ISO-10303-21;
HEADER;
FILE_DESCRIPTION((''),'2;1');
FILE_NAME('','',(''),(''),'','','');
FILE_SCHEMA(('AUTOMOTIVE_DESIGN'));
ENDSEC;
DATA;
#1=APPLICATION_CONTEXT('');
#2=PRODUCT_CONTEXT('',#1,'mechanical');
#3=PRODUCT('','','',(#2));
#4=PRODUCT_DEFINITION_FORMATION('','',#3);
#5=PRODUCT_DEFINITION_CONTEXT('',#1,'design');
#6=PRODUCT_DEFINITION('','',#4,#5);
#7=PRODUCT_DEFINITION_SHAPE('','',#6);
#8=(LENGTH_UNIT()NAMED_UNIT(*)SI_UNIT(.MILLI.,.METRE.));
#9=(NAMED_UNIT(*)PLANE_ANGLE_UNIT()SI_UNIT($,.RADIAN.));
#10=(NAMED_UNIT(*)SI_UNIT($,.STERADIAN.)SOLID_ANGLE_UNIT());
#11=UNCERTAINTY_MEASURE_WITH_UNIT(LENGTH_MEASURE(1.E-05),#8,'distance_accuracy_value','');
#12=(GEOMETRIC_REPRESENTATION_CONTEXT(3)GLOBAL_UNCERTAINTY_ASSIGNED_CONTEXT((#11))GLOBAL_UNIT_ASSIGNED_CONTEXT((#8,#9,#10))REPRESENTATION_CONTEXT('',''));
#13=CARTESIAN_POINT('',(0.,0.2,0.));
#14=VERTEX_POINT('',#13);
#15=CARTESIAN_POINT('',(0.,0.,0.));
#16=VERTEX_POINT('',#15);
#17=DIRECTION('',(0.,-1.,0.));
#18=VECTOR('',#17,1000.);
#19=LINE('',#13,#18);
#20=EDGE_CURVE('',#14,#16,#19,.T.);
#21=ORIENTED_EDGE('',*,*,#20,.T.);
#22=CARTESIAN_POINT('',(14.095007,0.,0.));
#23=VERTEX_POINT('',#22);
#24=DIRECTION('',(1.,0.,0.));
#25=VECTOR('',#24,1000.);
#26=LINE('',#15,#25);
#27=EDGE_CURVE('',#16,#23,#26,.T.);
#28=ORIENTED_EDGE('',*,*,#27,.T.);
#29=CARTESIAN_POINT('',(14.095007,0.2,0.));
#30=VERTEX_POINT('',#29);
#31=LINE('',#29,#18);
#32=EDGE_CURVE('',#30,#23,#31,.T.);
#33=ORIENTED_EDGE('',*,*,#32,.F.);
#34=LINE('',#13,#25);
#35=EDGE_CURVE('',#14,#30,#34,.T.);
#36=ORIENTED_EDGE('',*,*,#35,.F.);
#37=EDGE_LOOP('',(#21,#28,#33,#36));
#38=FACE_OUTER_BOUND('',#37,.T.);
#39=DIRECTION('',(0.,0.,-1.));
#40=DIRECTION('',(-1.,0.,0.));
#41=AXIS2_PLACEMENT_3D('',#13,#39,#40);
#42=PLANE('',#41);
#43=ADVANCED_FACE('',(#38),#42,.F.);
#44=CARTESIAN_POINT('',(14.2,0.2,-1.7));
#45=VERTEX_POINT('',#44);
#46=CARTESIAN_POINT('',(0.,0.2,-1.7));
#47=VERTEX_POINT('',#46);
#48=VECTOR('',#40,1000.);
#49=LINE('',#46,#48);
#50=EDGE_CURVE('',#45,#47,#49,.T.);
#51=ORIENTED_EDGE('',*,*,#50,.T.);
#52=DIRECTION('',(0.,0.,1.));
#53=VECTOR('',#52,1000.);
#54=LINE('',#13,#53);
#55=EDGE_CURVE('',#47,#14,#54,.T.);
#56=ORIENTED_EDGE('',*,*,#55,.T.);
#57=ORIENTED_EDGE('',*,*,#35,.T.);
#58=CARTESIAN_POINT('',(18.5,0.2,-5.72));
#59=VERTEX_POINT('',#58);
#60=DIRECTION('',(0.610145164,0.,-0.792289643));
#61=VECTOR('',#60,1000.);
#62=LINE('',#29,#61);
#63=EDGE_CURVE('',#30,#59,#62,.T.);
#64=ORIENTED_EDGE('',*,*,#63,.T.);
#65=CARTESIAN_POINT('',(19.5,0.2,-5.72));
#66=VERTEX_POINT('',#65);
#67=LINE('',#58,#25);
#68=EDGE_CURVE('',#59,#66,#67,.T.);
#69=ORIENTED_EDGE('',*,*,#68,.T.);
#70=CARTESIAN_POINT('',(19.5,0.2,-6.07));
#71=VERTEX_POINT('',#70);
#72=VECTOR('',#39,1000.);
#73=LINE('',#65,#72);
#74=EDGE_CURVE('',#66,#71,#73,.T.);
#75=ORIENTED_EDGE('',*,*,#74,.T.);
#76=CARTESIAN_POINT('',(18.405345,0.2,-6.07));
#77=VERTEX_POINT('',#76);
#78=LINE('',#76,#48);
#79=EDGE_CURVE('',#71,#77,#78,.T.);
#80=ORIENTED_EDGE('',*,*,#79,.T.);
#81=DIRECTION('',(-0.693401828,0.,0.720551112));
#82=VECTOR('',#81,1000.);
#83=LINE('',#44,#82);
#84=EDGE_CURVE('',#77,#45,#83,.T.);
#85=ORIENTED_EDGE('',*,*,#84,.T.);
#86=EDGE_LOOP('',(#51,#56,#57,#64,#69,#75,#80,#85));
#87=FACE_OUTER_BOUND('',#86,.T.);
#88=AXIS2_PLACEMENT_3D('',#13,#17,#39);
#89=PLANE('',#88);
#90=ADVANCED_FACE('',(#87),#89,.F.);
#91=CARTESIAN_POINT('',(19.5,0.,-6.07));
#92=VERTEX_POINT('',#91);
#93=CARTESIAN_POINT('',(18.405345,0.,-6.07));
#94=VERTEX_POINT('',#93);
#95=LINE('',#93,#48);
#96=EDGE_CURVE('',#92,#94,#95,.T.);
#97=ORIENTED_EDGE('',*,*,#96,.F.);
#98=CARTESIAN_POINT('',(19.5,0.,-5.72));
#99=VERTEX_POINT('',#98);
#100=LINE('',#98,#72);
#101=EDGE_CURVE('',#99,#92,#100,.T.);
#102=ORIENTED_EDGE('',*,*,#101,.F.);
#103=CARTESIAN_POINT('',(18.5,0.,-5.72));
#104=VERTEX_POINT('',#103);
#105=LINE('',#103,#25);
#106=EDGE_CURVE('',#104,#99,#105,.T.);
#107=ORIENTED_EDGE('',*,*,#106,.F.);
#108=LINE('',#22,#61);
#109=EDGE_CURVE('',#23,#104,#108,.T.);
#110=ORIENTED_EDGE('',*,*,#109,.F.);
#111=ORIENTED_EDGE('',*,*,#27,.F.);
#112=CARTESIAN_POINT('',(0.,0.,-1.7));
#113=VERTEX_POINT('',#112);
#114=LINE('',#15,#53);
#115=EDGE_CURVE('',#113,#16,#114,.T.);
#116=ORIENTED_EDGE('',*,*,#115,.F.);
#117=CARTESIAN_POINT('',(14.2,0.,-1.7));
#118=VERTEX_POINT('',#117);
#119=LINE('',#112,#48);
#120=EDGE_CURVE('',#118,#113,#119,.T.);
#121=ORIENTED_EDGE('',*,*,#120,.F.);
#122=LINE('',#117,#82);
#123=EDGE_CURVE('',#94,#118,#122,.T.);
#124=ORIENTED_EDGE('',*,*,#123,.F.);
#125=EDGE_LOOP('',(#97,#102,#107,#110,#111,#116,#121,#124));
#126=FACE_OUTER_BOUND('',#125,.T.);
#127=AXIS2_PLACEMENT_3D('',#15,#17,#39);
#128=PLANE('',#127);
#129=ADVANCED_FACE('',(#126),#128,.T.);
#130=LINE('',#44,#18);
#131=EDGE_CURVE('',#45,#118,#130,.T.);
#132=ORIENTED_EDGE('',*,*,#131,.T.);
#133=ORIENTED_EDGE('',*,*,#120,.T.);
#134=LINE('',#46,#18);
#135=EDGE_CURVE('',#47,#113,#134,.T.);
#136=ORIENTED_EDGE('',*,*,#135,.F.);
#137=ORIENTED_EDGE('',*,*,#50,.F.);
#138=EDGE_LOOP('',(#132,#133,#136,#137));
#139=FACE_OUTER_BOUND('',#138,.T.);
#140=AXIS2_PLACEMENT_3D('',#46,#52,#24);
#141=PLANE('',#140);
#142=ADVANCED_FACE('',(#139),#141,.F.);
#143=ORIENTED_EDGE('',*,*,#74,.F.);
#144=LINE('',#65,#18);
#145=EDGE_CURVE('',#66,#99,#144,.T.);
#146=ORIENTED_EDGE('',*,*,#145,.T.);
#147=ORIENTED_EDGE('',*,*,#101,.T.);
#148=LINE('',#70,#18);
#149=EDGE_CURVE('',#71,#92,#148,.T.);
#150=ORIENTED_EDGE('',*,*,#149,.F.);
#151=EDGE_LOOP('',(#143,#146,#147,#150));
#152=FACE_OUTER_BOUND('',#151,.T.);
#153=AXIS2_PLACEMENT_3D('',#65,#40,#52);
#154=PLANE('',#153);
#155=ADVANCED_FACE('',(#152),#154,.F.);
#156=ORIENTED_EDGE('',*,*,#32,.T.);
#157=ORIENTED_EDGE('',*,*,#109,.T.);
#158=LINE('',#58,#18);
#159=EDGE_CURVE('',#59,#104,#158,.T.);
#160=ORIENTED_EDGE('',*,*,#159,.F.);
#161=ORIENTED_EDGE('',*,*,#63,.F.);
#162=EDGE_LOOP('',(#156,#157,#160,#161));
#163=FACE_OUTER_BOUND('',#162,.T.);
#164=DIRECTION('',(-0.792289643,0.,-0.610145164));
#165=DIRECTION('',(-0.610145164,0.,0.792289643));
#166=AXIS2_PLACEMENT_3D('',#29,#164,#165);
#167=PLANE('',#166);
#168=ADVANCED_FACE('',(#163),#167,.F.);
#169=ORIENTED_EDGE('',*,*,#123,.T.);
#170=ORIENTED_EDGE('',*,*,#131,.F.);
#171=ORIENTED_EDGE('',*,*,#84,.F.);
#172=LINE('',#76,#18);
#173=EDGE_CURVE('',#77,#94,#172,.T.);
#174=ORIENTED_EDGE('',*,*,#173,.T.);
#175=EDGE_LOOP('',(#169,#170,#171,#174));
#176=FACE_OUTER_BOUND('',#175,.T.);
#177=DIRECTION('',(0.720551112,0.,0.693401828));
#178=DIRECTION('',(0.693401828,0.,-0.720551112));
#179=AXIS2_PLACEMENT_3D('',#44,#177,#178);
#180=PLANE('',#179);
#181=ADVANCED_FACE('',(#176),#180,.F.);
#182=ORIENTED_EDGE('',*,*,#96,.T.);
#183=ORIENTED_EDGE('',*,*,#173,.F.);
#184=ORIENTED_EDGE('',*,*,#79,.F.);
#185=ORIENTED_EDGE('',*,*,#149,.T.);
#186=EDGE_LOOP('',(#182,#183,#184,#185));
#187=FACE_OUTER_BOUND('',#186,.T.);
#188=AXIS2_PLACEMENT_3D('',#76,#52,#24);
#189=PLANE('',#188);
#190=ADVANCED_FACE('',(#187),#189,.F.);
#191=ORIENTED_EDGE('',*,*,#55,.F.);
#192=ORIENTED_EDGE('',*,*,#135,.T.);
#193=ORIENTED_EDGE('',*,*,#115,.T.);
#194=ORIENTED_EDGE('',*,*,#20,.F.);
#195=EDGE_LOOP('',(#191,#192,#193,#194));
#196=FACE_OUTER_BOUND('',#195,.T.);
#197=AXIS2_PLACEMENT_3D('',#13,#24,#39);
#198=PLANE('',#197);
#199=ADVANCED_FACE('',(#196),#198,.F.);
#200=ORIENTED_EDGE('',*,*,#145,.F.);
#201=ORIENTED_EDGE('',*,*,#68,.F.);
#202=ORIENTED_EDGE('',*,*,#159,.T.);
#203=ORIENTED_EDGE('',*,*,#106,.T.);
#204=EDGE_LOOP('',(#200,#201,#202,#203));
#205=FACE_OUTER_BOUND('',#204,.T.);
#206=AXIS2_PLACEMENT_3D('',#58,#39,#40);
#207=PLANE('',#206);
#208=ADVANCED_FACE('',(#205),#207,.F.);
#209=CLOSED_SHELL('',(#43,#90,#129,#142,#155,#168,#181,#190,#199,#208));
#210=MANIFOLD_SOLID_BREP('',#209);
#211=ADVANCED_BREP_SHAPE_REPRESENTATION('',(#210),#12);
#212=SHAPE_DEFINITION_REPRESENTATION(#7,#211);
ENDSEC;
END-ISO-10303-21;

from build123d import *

# Parameters (mm, degrees)
BOSS_EXTRUDE1_DEPTH = 0.2


with BuildPart() as part:
    # Sketch1 → Boss-Extrude1 (new body)
    with BuildSketch(Plane(origin=(0, 0, 0), x_dir=(1, 0, 0), z_dir=(0, 1, 0))):
        Polygon((14.2, 1.7), (18.405344965, 6.07), (19.5, 6.07), (19.5, 5.72), (18.5, 5.72), (14.095006994, 0), (0, 0), (0, 1.7), align=None)
    extrude(amount=BOSS_EXTRUDE1_DEPTH)


solid = part.part
